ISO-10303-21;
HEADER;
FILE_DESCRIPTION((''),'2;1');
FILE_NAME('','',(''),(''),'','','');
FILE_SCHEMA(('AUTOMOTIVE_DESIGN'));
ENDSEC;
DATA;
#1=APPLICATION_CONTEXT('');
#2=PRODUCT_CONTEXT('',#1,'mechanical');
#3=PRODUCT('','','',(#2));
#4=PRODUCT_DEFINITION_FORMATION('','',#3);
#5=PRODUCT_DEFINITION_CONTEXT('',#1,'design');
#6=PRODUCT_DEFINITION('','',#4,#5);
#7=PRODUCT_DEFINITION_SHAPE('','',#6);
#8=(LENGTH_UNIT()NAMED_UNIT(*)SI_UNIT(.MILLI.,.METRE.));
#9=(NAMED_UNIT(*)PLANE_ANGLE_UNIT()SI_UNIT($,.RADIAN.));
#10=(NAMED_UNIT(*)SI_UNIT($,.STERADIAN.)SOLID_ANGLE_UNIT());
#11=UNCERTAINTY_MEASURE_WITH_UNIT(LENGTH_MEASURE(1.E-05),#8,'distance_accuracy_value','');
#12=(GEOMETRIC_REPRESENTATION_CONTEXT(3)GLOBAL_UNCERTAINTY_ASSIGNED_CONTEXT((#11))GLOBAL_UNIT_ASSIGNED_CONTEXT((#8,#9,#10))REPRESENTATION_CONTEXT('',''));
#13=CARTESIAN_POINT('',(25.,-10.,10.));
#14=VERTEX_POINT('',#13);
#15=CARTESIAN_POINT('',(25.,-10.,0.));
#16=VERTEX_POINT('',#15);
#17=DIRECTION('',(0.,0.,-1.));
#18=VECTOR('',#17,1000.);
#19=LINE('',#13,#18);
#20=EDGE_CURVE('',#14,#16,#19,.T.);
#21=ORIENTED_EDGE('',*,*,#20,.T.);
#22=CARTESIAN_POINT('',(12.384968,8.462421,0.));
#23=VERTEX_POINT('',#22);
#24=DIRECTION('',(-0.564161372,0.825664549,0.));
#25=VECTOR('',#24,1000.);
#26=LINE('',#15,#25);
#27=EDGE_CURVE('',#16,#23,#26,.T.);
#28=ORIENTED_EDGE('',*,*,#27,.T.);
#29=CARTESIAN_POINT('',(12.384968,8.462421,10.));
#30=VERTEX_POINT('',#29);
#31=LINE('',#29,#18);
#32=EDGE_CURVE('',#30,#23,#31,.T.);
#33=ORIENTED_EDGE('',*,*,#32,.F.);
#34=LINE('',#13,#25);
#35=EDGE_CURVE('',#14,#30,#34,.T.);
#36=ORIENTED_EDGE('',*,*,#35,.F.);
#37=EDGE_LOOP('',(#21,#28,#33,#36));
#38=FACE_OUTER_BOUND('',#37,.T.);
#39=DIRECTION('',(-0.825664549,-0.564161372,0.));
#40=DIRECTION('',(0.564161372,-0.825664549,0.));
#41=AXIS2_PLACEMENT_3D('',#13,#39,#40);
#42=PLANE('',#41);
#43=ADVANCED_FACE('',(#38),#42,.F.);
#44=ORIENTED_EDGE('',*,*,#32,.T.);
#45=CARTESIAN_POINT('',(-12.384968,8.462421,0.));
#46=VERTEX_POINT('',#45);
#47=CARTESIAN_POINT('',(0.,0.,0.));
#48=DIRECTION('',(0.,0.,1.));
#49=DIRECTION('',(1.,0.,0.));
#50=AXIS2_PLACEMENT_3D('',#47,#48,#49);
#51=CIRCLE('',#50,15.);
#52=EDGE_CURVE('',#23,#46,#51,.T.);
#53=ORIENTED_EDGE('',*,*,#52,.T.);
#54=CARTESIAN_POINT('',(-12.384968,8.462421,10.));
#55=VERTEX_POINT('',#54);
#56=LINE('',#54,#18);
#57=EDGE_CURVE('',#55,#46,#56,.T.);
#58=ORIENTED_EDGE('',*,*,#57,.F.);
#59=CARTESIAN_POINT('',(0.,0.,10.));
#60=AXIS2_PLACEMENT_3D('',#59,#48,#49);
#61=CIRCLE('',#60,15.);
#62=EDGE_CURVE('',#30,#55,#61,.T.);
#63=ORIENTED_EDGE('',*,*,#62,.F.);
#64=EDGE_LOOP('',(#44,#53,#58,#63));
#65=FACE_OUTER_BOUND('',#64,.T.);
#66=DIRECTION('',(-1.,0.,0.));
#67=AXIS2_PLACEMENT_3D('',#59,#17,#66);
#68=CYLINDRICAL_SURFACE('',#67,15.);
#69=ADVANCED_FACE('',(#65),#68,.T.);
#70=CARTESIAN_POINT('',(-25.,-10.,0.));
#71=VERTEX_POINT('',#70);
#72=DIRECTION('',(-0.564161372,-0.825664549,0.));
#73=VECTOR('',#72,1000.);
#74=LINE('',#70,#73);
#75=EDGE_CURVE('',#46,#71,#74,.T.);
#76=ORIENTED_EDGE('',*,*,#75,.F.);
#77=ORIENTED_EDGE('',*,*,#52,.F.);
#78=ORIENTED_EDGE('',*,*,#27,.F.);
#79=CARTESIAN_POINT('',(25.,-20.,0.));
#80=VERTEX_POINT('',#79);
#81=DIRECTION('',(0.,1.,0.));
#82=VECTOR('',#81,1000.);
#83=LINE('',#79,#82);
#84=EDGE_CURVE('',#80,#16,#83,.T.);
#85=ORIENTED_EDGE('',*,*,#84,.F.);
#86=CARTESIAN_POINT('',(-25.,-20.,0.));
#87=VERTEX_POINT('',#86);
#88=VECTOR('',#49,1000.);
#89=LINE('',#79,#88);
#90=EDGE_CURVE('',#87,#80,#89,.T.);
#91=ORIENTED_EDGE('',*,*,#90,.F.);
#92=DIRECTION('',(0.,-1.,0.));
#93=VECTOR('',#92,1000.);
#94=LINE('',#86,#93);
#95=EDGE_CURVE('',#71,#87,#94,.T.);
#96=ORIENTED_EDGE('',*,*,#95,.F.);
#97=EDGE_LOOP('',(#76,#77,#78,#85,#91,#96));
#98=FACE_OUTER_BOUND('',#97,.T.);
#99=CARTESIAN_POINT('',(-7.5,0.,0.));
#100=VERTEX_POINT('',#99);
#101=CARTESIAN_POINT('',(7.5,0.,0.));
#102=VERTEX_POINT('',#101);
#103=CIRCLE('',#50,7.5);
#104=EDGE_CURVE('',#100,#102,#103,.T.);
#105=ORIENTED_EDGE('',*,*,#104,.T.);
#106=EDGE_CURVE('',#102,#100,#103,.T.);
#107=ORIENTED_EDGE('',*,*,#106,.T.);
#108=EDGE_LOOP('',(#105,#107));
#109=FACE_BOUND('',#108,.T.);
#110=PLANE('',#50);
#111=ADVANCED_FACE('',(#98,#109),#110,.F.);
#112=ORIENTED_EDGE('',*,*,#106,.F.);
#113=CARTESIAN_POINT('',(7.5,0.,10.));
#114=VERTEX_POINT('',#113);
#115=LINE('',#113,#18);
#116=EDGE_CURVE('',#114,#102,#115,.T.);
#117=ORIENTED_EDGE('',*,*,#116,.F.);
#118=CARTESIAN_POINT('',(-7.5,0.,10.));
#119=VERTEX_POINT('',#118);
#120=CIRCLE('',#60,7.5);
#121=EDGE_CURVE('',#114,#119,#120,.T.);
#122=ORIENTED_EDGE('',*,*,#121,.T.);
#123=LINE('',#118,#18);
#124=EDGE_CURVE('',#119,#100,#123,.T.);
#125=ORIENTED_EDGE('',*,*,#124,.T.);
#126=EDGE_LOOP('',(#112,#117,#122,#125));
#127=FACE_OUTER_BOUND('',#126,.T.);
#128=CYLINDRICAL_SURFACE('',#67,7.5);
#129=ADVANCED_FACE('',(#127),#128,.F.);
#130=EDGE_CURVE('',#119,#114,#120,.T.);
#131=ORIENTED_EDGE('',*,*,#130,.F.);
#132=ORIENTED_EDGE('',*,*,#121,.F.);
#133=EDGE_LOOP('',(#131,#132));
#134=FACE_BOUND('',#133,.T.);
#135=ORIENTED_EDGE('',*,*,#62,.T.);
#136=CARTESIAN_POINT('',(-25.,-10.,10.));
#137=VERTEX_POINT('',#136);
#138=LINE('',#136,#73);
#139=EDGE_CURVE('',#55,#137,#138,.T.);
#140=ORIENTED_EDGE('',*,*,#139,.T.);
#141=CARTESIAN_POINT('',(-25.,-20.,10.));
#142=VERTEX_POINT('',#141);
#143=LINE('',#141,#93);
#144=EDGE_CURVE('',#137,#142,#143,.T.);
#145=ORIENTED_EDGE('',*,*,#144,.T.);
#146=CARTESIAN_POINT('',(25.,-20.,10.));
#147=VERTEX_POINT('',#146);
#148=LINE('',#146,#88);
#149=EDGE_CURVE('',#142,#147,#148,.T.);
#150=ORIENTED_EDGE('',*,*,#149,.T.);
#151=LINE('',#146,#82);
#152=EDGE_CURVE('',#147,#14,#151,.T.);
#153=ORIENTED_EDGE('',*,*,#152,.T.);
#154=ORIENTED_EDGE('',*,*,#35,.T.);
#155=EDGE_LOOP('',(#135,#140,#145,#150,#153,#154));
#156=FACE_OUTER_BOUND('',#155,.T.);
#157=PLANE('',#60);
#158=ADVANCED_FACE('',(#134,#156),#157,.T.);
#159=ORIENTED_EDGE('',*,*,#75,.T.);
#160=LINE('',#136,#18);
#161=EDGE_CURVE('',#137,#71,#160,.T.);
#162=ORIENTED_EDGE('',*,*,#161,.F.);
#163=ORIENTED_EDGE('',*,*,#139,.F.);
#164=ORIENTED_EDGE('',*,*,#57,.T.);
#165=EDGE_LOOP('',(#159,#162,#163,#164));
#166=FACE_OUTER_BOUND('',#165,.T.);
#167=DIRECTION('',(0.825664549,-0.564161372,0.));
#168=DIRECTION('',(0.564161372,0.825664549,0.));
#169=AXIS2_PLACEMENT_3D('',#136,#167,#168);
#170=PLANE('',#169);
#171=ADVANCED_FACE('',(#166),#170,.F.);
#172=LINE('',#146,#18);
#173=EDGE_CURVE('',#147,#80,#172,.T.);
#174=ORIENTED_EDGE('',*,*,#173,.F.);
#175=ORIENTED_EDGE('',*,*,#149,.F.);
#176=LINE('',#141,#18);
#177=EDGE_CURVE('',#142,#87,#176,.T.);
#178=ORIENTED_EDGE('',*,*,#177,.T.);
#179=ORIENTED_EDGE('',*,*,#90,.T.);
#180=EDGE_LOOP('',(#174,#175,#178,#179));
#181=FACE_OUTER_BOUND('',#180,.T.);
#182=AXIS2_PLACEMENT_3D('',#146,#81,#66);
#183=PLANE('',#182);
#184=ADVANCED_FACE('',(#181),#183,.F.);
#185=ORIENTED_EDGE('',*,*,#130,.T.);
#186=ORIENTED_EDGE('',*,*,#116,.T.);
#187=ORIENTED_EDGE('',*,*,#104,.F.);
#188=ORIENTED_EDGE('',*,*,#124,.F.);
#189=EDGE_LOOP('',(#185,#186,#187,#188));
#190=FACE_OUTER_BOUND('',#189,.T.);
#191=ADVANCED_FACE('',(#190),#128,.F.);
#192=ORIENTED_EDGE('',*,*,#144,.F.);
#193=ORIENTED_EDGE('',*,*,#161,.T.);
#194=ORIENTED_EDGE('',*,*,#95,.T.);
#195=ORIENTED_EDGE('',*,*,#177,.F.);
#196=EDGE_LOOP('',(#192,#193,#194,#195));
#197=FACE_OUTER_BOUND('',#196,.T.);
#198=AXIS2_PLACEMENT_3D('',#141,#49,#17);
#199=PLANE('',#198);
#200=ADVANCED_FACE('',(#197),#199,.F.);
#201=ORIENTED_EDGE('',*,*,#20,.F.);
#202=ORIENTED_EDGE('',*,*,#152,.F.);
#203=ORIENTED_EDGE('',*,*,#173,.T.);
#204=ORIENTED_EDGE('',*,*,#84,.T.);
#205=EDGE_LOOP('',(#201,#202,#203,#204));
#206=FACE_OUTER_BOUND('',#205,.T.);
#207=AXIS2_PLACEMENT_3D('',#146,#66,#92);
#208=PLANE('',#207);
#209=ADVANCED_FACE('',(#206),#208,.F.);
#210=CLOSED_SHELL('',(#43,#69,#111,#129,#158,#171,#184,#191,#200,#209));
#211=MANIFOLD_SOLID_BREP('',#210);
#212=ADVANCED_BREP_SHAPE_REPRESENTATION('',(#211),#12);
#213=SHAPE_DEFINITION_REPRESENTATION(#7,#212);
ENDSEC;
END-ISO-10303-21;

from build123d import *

# Parameters (mm, degrees)
SKETCH_1_R      = 7.5
EXTRUDE_1_DEPTH = 10


with BuildPart() as part:
    # 草图1 → 凸台-拉伸1 (new body)
    with BuildSketch(Plane.XY):
        with BuildLine():
            Line((25, -20), (-25, -20))
            Line((-25, -20), (-25, -10))
            Line((-25, -10), (-12.384968229, 8.462420573))
            ThreePointArc((-12.384968229, 8.462420573), (0, 15), (12.384968229, 8.462420573))
            Line((12.384968229, 8.462420573), (25, -10))
            Line((25, -10), (25, -20))
        make_face()
        Circle(SKETCH_1_R, mode=Mode.SUBTRACT)
    extrude(amount=EXTRUDE_1_DEPTH)


solid = part.part
